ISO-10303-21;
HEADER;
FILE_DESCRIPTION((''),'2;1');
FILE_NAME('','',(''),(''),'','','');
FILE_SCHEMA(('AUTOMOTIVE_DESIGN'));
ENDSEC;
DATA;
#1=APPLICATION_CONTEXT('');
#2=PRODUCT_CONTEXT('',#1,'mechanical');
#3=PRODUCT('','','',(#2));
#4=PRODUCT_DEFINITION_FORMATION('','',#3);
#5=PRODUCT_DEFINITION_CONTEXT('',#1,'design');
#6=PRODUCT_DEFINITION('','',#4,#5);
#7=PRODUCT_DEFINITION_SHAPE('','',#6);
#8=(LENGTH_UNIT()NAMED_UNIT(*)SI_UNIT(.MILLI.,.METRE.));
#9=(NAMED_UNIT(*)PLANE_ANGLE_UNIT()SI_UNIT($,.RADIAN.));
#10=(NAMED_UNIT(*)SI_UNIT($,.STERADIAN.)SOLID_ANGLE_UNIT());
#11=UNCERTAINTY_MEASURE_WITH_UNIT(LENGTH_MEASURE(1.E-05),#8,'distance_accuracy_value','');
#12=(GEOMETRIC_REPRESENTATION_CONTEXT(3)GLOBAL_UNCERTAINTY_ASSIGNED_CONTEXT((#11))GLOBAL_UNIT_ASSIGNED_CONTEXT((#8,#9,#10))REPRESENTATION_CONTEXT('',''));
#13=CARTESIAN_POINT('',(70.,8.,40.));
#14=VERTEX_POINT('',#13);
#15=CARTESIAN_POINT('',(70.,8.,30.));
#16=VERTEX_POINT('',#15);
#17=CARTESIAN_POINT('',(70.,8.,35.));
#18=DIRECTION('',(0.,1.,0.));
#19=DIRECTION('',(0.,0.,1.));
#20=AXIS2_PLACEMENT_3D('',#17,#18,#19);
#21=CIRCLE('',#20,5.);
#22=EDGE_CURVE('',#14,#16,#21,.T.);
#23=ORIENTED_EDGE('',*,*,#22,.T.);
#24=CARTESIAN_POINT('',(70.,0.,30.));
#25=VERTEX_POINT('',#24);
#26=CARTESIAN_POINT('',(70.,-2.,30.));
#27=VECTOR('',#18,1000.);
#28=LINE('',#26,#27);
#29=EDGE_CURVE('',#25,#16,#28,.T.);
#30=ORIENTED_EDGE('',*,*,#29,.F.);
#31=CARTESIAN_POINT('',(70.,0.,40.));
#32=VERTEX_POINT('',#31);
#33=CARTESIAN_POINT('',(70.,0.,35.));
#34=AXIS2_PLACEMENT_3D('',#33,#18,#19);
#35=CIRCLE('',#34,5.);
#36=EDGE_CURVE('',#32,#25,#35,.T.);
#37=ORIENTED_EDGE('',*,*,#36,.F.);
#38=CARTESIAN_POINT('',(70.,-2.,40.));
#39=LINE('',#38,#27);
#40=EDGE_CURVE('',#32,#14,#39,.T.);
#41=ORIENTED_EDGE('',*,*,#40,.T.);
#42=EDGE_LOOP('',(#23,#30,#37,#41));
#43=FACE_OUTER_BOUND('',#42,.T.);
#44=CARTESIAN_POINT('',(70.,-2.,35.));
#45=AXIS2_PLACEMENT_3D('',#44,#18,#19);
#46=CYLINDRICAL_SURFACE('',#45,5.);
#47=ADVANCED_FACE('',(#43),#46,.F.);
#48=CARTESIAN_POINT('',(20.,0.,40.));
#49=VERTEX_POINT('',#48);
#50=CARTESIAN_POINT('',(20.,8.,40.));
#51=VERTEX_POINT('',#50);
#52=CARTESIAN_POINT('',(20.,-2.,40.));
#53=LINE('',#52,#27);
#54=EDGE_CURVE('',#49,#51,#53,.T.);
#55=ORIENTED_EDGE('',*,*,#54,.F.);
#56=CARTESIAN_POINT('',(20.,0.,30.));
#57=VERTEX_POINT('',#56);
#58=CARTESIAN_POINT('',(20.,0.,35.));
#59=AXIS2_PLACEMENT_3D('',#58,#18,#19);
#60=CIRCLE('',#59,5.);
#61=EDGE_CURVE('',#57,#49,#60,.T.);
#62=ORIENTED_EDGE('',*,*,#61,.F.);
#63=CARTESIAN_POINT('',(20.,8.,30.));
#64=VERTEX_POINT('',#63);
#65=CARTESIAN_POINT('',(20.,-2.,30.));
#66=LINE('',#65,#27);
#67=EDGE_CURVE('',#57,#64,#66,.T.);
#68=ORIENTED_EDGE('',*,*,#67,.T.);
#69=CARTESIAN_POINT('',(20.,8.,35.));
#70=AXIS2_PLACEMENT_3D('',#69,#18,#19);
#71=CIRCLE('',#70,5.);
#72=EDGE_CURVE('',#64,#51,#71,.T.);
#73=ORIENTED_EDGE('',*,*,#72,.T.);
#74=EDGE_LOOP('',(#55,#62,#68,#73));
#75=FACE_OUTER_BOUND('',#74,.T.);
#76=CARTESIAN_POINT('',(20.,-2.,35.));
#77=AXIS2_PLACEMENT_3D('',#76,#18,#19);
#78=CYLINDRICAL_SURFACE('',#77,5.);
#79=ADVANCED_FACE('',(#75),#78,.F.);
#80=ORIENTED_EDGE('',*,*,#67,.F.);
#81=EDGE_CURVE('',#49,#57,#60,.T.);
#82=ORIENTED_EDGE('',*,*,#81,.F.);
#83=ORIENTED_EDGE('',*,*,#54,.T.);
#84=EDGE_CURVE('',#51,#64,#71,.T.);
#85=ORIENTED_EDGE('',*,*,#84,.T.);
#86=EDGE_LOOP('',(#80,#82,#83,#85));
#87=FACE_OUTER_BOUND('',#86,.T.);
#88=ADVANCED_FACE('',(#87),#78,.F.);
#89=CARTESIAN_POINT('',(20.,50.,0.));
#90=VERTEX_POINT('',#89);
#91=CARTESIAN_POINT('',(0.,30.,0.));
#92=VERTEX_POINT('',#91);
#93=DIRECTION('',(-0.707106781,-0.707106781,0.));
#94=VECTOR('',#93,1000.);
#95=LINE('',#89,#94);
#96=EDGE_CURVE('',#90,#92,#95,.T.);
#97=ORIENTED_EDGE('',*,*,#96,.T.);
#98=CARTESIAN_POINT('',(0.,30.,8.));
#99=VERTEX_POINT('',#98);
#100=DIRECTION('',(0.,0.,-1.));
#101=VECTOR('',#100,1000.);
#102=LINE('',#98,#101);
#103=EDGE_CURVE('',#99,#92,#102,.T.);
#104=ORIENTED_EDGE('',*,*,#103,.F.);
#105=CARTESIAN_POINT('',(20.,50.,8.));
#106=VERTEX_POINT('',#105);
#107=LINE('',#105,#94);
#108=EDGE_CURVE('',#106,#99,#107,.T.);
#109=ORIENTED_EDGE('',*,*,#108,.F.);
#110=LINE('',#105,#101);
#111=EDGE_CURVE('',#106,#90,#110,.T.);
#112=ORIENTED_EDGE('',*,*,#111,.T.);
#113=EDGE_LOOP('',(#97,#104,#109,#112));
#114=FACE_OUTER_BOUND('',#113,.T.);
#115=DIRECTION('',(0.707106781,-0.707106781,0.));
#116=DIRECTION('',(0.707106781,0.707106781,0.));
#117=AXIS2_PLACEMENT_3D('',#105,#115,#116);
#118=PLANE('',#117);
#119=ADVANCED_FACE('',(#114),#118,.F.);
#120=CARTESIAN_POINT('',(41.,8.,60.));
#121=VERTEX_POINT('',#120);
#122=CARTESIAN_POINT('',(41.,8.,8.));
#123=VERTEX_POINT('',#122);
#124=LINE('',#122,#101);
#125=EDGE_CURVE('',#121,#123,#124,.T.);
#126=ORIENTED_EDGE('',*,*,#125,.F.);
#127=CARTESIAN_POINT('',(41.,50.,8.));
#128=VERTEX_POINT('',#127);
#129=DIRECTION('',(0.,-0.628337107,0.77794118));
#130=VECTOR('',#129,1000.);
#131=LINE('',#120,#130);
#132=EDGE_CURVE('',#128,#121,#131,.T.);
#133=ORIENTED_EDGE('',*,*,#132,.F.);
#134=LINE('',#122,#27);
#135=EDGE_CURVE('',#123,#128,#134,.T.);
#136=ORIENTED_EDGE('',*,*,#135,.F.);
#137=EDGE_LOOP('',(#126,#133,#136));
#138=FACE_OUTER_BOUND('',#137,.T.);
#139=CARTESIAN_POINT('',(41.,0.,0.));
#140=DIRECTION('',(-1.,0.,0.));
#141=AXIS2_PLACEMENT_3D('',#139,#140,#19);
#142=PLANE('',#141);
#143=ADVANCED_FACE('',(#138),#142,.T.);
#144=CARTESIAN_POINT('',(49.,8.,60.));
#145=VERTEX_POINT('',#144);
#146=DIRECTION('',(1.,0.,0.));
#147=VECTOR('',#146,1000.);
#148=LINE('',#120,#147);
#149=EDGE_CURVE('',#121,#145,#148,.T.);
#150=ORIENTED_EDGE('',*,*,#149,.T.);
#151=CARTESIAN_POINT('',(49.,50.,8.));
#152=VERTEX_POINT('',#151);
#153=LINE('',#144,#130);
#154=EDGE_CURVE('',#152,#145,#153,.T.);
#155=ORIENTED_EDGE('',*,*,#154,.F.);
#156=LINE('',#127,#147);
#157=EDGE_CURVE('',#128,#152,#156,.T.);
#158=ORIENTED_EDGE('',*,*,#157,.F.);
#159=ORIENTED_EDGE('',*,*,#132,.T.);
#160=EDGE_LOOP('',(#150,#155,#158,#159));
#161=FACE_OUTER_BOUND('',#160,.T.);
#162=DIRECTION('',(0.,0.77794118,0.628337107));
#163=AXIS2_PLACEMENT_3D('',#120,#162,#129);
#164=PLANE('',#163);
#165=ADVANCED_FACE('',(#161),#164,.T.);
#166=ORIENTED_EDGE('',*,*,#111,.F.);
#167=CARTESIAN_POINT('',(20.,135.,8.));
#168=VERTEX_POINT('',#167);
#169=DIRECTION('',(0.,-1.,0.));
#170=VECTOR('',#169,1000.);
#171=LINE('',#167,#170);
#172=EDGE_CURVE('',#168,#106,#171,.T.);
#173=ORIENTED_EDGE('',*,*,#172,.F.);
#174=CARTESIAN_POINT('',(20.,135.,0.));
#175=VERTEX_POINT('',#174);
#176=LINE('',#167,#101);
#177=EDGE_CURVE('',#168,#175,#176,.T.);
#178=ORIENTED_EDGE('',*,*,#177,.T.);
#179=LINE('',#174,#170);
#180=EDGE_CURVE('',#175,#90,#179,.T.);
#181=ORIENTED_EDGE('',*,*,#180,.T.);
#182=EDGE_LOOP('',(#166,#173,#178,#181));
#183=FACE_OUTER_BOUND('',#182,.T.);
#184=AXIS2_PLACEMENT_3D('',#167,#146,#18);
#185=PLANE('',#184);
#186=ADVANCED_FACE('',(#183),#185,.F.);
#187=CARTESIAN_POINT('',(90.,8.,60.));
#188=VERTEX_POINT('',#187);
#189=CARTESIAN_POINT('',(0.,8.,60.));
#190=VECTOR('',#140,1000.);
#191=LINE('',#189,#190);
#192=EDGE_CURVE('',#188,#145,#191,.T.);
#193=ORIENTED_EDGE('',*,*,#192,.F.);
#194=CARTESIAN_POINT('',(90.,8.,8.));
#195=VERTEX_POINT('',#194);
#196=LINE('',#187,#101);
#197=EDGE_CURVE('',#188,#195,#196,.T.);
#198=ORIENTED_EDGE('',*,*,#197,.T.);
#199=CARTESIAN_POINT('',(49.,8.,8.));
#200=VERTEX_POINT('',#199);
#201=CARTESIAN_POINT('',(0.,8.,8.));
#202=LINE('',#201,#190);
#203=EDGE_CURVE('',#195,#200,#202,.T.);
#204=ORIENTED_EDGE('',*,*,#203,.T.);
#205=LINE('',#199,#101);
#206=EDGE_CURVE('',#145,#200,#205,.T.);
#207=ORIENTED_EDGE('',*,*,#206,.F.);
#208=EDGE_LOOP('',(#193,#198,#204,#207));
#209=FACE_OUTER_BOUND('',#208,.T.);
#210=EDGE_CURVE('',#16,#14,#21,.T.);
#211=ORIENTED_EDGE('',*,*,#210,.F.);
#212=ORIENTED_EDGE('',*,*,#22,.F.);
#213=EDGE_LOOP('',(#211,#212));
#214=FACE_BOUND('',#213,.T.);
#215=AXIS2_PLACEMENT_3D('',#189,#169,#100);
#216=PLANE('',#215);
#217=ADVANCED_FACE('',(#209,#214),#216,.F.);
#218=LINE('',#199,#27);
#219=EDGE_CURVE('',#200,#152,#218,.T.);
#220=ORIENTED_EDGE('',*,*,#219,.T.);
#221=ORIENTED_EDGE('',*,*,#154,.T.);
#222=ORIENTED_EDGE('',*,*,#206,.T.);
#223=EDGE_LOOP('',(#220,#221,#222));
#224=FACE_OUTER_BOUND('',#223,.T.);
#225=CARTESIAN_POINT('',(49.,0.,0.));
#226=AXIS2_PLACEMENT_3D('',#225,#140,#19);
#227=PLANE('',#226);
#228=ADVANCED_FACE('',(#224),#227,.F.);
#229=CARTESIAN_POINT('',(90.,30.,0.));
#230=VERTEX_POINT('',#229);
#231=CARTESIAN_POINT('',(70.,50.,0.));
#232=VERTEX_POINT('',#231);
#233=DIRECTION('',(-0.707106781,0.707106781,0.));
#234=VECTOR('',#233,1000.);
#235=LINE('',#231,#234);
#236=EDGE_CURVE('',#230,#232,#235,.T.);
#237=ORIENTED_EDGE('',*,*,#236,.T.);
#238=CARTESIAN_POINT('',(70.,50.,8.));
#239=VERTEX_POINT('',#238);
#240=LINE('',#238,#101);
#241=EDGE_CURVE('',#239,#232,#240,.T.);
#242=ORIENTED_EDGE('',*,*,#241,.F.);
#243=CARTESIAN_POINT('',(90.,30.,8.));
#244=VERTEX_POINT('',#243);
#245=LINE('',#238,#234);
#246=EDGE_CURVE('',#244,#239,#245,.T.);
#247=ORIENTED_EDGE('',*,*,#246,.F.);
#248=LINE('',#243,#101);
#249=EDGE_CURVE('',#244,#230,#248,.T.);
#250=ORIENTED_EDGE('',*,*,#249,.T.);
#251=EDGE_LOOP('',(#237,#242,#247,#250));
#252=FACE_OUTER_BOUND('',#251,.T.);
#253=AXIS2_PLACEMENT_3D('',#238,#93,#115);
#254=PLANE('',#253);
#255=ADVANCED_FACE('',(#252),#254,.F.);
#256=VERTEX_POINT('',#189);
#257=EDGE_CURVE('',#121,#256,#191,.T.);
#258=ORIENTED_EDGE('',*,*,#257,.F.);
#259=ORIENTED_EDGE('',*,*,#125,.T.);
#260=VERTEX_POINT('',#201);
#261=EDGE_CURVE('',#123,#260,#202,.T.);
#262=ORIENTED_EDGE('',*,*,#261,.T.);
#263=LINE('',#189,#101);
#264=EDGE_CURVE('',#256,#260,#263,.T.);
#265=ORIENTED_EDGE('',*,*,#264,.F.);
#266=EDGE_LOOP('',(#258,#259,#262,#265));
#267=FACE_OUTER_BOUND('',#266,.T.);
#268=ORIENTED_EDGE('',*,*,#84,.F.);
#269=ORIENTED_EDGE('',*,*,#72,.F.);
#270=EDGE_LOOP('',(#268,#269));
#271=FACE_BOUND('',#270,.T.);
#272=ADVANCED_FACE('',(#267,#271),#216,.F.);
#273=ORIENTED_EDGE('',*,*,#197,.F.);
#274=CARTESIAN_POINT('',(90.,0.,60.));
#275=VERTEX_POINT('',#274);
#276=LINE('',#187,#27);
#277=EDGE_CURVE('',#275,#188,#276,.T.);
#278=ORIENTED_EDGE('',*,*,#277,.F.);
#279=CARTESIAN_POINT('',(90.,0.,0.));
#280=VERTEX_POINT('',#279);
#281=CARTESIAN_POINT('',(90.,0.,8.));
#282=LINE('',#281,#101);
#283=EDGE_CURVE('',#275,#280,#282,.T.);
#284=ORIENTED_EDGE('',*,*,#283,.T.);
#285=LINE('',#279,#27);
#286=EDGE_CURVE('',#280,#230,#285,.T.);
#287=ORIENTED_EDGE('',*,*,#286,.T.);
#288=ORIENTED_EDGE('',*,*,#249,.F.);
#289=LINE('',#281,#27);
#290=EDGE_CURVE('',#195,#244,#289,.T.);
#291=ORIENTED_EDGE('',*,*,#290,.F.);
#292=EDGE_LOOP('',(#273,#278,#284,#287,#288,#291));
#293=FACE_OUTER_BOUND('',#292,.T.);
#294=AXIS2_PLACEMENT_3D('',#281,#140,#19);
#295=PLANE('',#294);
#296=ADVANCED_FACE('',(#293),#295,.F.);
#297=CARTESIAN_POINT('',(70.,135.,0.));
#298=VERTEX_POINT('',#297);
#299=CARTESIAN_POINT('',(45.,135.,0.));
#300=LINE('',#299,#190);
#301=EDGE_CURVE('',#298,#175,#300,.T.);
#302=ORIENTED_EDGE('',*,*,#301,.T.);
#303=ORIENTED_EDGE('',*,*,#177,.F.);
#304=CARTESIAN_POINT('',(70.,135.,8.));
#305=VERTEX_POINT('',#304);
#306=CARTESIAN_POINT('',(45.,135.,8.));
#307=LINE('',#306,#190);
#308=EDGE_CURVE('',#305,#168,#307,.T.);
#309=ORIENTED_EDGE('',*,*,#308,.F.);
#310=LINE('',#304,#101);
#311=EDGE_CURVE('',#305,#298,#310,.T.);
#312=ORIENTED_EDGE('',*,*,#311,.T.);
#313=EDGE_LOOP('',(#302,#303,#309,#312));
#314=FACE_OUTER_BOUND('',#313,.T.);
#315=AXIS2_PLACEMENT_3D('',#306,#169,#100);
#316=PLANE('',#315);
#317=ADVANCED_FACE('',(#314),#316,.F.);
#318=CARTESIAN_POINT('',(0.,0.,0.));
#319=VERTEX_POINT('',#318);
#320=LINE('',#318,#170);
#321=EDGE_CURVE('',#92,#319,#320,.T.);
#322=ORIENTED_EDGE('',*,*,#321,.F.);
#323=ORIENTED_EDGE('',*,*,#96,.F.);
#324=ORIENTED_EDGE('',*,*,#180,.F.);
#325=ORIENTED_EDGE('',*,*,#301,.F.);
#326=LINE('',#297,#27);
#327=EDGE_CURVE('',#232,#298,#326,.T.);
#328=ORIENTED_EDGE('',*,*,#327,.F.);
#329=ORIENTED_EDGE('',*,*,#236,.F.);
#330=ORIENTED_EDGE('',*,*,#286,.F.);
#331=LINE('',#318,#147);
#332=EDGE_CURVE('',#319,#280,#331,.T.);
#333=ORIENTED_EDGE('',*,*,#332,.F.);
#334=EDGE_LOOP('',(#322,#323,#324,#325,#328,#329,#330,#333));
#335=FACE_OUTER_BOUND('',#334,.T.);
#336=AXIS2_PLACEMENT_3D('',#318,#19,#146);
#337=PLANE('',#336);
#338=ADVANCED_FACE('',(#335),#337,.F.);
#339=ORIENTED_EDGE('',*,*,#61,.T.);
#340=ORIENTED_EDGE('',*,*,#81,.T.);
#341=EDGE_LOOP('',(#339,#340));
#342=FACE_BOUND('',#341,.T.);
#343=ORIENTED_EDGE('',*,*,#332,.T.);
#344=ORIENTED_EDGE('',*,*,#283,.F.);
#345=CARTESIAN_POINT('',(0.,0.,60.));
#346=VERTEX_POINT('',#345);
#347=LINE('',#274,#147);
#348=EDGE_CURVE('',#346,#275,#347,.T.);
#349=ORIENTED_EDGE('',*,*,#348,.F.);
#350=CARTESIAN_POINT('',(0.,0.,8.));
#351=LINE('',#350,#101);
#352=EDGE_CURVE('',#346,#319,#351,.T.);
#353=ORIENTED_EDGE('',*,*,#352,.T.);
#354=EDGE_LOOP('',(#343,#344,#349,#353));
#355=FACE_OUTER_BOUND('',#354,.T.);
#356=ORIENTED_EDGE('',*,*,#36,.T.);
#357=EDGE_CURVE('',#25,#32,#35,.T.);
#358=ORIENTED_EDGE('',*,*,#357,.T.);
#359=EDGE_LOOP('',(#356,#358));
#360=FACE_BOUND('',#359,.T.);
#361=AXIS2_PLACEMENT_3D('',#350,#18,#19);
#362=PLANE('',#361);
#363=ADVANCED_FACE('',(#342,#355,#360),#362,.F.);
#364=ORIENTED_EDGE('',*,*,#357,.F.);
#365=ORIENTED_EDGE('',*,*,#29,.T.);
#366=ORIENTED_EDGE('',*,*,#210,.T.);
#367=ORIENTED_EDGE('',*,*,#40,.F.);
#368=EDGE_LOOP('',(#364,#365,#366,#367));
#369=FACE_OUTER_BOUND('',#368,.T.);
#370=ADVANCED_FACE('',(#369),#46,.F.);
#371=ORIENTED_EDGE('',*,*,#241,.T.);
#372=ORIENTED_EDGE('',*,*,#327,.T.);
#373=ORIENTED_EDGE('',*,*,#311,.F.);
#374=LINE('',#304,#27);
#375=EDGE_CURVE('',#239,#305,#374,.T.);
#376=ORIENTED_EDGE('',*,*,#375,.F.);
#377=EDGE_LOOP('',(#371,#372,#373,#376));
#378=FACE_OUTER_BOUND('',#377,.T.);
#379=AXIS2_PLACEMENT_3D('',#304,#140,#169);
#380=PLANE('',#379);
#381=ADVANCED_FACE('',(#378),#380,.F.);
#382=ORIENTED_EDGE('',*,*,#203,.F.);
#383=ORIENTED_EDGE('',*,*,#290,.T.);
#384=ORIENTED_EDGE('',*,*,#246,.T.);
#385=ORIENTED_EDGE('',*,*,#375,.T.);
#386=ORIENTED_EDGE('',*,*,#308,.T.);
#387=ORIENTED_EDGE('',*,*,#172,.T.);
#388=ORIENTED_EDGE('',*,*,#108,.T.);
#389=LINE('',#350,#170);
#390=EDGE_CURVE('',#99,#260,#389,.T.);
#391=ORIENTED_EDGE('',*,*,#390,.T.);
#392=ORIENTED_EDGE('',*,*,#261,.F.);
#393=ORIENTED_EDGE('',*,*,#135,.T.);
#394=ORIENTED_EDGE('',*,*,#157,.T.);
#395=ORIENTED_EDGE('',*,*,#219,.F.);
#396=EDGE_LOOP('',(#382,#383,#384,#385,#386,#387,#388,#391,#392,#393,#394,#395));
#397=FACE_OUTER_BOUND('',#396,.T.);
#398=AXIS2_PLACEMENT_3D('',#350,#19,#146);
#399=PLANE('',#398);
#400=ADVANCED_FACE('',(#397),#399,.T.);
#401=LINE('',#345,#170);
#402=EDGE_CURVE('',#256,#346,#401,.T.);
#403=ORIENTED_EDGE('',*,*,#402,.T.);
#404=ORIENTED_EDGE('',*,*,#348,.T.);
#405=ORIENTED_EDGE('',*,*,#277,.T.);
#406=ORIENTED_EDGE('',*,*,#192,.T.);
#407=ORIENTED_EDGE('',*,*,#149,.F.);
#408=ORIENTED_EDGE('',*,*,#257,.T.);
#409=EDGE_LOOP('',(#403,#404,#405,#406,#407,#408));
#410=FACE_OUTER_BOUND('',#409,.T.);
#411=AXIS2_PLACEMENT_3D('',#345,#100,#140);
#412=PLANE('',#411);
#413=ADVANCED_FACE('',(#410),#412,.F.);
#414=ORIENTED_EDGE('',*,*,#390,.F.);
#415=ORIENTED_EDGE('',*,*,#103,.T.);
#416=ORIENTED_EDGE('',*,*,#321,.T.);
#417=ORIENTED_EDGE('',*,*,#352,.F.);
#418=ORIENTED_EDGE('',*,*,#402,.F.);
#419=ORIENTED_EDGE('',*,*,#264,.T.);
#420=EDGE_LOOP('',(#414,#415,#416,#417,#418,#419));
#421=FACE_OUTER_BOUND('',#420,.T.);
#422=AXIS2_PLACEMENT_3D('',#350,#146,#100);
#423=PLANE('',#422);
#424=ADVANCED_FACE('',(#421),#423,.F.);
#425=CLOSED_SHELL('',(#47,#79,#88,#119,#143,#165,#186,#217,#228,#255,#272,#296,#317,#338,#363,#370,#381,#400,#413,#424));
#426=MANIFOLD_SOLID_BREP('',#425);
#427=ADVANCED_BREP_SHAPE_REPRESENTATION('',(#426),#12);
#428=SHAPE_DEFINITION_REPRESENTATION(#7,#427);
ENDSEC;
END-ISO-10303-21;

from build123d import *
from build123d.topology import SkipClean

# Parameters (mm, degrees)
EXTRUDE_2_DEPTH      = 8
SKETCH_2_W           = 90
SKETCH_2_H           = 8
EXTRUDE_3_DEPTH      = 52
EXTRUDE_4_DEPTH      = 4
EXTRUDE_4_DEPTH_BACK = 4
CUT_EXTRUDE_2_DEPTH  = 18
SKETCH_6_R           = 5
CUT_EXTRUDE_3_DEPTH  = 10
SKETCH_8_R           = 5
CUT_EXTRUDE_4_DEPTH  = 10
EXTRUDE_6_DEPTH      = 8


with BuildPart() as part:
    # 草图1 → 凸台-拉伸2 (new body)
    with BuildSketch(Plane.XY):
        Polygon((0, 0), (90, 0), (90, 30), (70, 50), (70, 135), (45, 135), (20, 135), (20, 50), (0, 30), align=None)
    extrude(amount=EXTRUDE_2_DEPTH)

    # 草图2 → 凸台-拉伸3 (add)
    with BuildSketch(Plane.XY.offset(8)):
        with Locations((45, 4)):
            Rectangle(SKETCH_2_W, SKETCH_2_H)
    extrude(amount=EXTRUDE_3_DEPTH)

    # 草图4 → 凸台-拉伸4 (add, two sides: drawn at the far end of the back side and taken through both)
    with BuildSketch(Plane(origin=(45, 0, 0), x_dir=(0, 0, -1), z_dir=(1, 0, 0)).offset(-EXTRUDE_4_DEPTH_BACK)):
        Polygon((-8, 8), (-8, 50), (-60, 8), align=None)
    extrude(amount=EXTRUDE_4_DEPTH + EXTRUDE_4_DEPTH_BACK)

    # 草图5 → 切除-拉伸2 (cut)
    with BuildSketch(Plane(origin=(0, 8, 0), x_dir=(1, 0, 0), z_dir=(0, 1, 0))):
        with BuildLine():
            ThreePointArc((70, -35), (65, -30), (60, -35))
            Line((60, -35), (65, -35))
            Line((65, -35), (70, -35))
        make_face()
        with BuildLine():
            Line((65, -35), (60, -35))
            ThreePointArc((60, -35), (65, -40), (70, -35))
            Line((70, -35), (65, -35))
        make_face()
        with BuildLine():
            Line((20, -35), (25, -35))
            Line((25, -35), (30, -35))
            ThreePointArc((30, -35), (25, -30), (20, -35))
        make_face()
        with BuildLine():
            Line((30, -35), (25, -35))
            Line((25, -35), (20, -35))
            ThreePointArc((20, -35), (25, -40), (30, -35))
        make_face()
    extrude(amount=-CUT_EXTRUDE_2_DEPTH, mode=Mode.SUBTRACT)

    # 草图6 → 切除-拉伸3 (cut)
    with BuildSketch(Plane(origin=(0, 8, 0), x_dir=(1, 0, 0), z_dir=(0, 1, 0))):
        with Locations((20, -35)):
            Circle(SKETCH_6_R)
    extrude(amount=-CUT_EXTRUDE_3_DEPTH, mode=Mode.SUBTRACT)

    # 草图8 → 切除-拉伸4 (cut)
    with BuildSketch(Plane(origin=(0, 8, 0), x_dir=(1, 0, 0), z_dir=(0, 1, 0))):
        with Locations((70, -35)):
            Circle(SKETCH_8_R)
        with Locations((65, -35)):
            Circle(SKETCH_8_R)
    extrude(amount=-CUT_EXTRUDE_4_DEPTH, mode=Mode.SUBTRACT)

    # 草图9 → 凸台-拉伸6 (add)
    with SkipClean():  # the faces are left unmerged after this step: merging them gives an invalid solid
        with BuildSketch(Plane(origin=(0, 8, 0), x_dir=(1, 0, 0), z_dir=(0, 1, 0))):
            with BuildLine():
                ThreePointArc((22.5, -30.669872981), (25, -35), (22.5, -39.330127019))
                ThreePointArc((22.5, -39.330127019), (30, -35), (22.5, -30.669872981))
            make_face()
            with BuildLine():
                ThreePointArc((67.5, -39.330127019), (65, -35), (67.5, -30.669872981))
                ThreePointArc((67.5, -30.669872981), (60, -35), (67.5, -39.330127019))
            make_face()
        extrude(amount=-EXTRUDE_6_DEPTH)


solid = part.part
